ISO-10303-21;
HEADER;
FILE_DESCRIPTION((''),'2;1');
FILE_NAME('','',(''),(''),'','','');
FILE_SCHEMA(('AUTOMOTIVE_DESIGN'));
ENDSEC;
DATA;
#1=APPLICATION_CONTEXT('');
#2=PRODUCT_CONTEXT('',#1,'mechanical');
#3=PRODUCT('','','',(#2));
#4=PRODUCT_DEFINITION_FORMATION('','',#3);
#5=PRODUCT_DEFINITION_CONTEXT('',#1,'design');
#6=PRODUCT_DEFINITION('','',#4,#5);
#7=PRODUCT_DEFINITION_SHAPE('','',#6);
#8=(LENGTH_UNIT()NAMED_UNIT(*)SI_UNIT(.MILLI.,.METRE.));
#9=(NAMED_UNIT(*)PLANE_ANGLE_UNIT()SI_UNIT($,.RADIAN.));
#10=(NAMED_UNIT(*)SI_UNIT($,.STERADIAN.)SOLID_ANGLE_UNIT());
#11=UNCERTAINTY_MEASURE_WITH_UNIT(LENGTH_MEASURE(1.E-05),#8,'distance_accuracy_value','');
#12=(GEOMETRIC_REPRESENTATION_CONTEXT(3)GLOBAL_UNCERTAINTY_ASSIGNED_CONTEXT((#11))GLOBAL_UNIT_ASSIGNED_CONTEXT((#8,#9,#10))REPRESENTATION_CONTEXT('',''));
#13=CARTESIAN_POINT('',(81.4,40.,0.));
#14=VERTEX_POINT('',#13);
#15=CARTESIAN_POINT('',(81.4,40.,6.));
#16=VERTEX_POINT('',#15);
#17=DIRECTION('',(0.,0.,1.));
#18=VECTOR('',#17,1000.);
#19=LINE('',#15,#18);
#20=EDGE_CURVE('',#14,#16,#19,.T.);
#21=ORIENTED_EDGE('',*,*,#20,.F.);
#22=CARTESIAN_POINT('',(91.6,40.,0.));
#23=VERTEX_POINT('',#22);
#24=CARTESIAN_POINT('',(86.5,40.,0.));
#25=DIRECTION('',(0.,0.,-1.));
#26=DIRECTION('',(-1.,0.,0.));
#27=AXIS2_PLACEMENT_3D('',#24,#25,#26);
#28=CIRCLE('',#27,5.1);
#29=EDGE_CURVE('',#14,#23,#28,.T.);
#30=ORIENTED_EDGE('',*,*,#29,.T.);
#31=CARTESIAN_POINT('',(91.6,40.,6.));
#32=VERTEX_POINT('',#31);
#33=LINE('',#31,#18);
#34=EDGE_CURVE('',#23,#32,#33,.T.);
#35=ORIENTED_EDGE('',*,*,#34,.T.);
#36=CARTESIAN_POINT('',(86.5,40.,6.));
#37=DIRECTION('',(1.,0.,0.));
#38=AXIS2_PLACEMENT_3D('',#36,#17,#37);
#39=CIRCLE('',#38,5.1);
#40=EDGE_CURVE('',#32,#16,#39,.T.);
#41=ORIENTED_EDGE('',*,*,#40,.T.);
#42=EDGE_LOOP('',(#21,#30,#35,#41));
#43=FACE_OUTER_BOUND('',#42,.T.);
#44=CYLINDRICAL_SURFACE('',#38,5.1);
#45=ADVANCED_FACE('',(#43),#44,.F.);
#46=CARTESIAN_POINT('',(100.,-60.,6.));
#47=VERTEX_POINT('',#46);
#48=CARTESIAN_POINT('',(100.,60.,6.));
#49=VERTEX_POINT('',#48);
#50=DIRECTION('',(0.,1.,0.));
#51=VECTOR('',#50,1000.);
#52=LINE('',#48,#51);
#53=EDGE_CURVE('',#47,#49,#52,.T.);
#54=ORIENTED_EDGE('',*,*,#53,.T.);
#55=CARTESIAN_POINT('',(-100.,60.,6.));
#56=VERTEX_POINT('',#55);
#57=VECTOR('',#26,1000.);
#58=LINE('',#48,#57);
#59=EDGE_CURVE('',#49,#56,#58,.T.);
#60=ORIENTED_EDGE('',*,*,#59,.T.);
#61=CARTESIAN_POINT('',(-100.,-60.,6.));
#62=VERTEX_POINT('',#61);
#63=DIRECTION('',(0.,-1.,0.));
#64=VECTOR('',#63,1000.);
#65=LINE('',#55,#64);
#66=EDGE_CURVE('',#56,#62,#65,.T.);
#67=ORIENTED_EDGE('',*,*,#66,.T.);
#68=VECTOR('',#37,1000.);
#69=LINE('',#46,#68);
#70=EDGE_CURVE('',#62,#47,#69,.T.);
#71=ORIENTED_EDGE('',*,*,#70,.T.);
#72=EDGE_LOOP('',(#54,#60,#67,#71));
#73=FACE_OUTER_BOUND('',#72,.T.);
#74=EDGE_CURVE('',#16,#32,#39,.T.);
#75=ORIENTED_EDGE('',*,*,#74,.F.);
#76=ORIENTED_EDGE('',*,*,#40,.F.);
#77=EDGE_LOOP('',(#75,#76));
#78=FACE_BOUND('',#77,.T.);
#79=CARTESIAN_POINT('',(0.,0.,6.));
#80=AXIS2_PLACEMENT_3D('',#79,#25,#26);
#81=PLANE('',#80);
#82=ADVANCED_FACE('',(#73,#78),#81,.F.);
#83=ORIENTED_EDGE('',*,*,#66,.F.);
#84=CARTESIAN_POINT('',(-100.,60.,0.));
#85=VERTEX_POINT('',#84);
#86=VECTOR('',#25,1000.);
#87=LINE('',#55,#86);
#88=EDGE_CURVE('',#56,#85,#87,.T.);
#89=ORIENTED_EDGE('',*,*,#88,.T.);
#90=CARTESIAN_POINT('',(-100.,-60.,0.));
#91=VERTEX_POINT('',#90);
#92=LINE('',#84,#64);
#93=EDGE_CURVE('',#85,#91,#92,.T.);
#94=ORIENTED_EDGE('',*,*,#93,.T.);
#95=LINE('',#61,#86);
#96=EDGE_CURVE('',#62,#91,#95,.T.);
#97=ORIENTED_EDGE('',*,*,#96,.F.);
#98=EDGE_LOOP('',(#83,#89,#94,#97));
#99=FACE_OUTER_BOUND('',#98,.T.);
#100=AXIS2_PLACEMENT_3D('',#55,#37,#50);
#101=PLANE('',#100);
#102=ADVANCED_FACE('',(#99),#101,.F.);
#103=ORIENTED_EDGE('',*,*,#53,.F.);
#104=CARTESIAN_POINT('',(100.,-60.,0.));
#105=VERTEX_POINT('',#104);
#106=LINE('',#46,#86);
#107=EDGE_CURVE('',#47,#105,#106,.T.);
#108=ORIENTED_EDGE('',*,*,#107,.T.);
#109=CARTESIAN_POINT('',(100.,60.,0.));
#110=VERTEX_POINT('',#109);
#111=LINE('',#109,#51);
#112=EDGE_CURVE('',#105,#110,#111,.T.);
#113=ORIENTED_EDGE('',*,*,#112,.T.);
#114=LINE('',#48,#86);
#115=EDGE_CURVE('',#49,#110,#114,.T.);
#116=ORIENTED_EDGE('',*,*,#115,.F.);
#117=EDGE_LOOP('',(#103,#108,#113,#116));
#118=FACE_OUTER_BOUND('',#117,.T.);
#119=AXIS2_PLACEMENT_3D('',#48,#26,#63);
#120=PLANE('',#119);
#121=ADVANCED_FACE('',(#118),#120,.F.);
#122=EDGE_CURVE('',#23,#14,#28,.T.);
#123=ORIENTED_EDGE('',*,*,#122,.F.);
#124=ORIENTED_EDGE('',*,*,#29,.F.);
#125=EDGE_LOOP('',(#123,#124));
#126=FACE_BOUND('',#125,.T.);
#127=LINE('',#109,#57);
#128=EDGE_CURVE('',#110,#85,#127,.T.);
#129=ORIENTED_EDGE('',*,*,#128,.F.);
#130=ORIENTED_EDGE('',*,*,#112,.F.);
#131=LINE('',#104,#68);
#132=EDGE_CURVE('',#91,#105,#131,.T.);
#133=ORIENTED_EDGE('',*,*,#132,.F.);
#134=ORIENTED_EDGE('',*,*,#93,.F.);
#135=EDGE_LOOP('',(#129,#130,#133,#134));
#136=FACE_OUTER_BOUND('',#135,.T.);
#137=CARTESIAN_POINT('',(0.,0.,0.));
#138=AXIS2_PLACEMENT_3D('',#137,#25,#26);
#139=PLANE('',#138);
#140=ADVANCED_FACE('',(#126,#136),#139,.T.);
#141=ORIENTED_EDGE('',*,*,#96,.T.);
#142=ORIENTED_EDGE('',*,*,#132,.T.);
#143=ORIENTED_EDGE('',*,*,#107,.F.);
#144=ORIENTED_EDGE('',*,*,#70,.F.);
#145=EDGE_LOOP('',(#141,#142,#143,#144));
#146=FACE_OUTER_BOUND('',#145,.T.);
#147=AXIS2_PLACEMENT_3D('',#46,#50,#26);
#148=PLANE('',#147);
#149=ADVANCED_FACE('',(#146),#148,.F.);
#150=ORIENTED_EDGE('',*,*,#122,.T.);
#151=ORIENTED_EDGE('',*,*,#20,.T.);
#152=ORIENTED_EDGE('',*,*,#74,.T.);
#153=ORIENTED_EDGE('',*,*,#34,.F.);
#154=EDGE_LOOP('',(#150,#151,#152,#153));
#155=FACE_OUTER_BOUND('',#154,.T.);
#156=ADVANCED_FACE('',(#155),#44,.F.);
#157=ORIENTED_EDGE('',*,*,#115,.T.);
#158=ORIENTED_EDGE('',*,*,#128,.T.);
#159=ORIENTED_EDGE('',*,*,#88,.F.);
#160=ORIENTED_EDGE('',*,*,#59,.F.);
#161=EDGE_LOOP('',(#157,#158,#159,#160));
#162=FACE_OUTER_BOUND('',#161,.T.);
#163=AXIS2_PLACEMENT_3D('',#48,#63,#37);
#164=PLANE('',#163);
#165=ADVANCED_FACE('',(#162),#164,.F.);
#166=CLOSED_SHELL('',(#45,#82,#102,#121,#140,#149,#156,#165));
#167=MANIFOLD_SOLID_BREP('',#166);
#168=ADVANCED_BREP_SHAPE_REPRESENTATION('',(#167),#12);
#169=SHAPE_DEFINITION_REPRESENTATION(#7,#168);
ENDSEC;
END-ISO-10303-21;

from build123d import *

# Parameters (mm, degrees)
SKETCH1_W              = 200
SKETCH1_H              = 120
BOSS_EXTRUDE1_DEPTH    = 6
M12_TAPPED_HOLE1_D     = 10.2
M12_TAPPED_HOLE1_DEPTH = 29.25
M12_TAPPED_HOLE1_TIP   = 3.064389157


with BuildPart() as part:
    # Sketch1 → Boss-Extrude1 (new body)
    with BuildSketch(Plane.XY):
        Rectangle(SKETCH1_W, SKETCH1_H)
    extrude(amount=BOSS_EXTRUDE1_DEPTH)

    # M12 Tapped Hole1
    with Locations(Plane.XY.offset(6)):
        with Locations((86.5, 40)):
            Hole(M12_TAPPED_HOLE1_D / 2, depth=M12_TAPPED_HOLE1_DEPTH)
            with Locations((0, 0, -(M12_TAPPED_HOLE1_DEPTH + M12_TAPPED_HOLE1_TIP / 2))):  # 118° drill point
                Cone(0, M12_TAPPED_HOLE1_D / 2, M12_TAPPED_HOLE1_TIP, mode=Mode.SUBTRACT)


solid = part.part
